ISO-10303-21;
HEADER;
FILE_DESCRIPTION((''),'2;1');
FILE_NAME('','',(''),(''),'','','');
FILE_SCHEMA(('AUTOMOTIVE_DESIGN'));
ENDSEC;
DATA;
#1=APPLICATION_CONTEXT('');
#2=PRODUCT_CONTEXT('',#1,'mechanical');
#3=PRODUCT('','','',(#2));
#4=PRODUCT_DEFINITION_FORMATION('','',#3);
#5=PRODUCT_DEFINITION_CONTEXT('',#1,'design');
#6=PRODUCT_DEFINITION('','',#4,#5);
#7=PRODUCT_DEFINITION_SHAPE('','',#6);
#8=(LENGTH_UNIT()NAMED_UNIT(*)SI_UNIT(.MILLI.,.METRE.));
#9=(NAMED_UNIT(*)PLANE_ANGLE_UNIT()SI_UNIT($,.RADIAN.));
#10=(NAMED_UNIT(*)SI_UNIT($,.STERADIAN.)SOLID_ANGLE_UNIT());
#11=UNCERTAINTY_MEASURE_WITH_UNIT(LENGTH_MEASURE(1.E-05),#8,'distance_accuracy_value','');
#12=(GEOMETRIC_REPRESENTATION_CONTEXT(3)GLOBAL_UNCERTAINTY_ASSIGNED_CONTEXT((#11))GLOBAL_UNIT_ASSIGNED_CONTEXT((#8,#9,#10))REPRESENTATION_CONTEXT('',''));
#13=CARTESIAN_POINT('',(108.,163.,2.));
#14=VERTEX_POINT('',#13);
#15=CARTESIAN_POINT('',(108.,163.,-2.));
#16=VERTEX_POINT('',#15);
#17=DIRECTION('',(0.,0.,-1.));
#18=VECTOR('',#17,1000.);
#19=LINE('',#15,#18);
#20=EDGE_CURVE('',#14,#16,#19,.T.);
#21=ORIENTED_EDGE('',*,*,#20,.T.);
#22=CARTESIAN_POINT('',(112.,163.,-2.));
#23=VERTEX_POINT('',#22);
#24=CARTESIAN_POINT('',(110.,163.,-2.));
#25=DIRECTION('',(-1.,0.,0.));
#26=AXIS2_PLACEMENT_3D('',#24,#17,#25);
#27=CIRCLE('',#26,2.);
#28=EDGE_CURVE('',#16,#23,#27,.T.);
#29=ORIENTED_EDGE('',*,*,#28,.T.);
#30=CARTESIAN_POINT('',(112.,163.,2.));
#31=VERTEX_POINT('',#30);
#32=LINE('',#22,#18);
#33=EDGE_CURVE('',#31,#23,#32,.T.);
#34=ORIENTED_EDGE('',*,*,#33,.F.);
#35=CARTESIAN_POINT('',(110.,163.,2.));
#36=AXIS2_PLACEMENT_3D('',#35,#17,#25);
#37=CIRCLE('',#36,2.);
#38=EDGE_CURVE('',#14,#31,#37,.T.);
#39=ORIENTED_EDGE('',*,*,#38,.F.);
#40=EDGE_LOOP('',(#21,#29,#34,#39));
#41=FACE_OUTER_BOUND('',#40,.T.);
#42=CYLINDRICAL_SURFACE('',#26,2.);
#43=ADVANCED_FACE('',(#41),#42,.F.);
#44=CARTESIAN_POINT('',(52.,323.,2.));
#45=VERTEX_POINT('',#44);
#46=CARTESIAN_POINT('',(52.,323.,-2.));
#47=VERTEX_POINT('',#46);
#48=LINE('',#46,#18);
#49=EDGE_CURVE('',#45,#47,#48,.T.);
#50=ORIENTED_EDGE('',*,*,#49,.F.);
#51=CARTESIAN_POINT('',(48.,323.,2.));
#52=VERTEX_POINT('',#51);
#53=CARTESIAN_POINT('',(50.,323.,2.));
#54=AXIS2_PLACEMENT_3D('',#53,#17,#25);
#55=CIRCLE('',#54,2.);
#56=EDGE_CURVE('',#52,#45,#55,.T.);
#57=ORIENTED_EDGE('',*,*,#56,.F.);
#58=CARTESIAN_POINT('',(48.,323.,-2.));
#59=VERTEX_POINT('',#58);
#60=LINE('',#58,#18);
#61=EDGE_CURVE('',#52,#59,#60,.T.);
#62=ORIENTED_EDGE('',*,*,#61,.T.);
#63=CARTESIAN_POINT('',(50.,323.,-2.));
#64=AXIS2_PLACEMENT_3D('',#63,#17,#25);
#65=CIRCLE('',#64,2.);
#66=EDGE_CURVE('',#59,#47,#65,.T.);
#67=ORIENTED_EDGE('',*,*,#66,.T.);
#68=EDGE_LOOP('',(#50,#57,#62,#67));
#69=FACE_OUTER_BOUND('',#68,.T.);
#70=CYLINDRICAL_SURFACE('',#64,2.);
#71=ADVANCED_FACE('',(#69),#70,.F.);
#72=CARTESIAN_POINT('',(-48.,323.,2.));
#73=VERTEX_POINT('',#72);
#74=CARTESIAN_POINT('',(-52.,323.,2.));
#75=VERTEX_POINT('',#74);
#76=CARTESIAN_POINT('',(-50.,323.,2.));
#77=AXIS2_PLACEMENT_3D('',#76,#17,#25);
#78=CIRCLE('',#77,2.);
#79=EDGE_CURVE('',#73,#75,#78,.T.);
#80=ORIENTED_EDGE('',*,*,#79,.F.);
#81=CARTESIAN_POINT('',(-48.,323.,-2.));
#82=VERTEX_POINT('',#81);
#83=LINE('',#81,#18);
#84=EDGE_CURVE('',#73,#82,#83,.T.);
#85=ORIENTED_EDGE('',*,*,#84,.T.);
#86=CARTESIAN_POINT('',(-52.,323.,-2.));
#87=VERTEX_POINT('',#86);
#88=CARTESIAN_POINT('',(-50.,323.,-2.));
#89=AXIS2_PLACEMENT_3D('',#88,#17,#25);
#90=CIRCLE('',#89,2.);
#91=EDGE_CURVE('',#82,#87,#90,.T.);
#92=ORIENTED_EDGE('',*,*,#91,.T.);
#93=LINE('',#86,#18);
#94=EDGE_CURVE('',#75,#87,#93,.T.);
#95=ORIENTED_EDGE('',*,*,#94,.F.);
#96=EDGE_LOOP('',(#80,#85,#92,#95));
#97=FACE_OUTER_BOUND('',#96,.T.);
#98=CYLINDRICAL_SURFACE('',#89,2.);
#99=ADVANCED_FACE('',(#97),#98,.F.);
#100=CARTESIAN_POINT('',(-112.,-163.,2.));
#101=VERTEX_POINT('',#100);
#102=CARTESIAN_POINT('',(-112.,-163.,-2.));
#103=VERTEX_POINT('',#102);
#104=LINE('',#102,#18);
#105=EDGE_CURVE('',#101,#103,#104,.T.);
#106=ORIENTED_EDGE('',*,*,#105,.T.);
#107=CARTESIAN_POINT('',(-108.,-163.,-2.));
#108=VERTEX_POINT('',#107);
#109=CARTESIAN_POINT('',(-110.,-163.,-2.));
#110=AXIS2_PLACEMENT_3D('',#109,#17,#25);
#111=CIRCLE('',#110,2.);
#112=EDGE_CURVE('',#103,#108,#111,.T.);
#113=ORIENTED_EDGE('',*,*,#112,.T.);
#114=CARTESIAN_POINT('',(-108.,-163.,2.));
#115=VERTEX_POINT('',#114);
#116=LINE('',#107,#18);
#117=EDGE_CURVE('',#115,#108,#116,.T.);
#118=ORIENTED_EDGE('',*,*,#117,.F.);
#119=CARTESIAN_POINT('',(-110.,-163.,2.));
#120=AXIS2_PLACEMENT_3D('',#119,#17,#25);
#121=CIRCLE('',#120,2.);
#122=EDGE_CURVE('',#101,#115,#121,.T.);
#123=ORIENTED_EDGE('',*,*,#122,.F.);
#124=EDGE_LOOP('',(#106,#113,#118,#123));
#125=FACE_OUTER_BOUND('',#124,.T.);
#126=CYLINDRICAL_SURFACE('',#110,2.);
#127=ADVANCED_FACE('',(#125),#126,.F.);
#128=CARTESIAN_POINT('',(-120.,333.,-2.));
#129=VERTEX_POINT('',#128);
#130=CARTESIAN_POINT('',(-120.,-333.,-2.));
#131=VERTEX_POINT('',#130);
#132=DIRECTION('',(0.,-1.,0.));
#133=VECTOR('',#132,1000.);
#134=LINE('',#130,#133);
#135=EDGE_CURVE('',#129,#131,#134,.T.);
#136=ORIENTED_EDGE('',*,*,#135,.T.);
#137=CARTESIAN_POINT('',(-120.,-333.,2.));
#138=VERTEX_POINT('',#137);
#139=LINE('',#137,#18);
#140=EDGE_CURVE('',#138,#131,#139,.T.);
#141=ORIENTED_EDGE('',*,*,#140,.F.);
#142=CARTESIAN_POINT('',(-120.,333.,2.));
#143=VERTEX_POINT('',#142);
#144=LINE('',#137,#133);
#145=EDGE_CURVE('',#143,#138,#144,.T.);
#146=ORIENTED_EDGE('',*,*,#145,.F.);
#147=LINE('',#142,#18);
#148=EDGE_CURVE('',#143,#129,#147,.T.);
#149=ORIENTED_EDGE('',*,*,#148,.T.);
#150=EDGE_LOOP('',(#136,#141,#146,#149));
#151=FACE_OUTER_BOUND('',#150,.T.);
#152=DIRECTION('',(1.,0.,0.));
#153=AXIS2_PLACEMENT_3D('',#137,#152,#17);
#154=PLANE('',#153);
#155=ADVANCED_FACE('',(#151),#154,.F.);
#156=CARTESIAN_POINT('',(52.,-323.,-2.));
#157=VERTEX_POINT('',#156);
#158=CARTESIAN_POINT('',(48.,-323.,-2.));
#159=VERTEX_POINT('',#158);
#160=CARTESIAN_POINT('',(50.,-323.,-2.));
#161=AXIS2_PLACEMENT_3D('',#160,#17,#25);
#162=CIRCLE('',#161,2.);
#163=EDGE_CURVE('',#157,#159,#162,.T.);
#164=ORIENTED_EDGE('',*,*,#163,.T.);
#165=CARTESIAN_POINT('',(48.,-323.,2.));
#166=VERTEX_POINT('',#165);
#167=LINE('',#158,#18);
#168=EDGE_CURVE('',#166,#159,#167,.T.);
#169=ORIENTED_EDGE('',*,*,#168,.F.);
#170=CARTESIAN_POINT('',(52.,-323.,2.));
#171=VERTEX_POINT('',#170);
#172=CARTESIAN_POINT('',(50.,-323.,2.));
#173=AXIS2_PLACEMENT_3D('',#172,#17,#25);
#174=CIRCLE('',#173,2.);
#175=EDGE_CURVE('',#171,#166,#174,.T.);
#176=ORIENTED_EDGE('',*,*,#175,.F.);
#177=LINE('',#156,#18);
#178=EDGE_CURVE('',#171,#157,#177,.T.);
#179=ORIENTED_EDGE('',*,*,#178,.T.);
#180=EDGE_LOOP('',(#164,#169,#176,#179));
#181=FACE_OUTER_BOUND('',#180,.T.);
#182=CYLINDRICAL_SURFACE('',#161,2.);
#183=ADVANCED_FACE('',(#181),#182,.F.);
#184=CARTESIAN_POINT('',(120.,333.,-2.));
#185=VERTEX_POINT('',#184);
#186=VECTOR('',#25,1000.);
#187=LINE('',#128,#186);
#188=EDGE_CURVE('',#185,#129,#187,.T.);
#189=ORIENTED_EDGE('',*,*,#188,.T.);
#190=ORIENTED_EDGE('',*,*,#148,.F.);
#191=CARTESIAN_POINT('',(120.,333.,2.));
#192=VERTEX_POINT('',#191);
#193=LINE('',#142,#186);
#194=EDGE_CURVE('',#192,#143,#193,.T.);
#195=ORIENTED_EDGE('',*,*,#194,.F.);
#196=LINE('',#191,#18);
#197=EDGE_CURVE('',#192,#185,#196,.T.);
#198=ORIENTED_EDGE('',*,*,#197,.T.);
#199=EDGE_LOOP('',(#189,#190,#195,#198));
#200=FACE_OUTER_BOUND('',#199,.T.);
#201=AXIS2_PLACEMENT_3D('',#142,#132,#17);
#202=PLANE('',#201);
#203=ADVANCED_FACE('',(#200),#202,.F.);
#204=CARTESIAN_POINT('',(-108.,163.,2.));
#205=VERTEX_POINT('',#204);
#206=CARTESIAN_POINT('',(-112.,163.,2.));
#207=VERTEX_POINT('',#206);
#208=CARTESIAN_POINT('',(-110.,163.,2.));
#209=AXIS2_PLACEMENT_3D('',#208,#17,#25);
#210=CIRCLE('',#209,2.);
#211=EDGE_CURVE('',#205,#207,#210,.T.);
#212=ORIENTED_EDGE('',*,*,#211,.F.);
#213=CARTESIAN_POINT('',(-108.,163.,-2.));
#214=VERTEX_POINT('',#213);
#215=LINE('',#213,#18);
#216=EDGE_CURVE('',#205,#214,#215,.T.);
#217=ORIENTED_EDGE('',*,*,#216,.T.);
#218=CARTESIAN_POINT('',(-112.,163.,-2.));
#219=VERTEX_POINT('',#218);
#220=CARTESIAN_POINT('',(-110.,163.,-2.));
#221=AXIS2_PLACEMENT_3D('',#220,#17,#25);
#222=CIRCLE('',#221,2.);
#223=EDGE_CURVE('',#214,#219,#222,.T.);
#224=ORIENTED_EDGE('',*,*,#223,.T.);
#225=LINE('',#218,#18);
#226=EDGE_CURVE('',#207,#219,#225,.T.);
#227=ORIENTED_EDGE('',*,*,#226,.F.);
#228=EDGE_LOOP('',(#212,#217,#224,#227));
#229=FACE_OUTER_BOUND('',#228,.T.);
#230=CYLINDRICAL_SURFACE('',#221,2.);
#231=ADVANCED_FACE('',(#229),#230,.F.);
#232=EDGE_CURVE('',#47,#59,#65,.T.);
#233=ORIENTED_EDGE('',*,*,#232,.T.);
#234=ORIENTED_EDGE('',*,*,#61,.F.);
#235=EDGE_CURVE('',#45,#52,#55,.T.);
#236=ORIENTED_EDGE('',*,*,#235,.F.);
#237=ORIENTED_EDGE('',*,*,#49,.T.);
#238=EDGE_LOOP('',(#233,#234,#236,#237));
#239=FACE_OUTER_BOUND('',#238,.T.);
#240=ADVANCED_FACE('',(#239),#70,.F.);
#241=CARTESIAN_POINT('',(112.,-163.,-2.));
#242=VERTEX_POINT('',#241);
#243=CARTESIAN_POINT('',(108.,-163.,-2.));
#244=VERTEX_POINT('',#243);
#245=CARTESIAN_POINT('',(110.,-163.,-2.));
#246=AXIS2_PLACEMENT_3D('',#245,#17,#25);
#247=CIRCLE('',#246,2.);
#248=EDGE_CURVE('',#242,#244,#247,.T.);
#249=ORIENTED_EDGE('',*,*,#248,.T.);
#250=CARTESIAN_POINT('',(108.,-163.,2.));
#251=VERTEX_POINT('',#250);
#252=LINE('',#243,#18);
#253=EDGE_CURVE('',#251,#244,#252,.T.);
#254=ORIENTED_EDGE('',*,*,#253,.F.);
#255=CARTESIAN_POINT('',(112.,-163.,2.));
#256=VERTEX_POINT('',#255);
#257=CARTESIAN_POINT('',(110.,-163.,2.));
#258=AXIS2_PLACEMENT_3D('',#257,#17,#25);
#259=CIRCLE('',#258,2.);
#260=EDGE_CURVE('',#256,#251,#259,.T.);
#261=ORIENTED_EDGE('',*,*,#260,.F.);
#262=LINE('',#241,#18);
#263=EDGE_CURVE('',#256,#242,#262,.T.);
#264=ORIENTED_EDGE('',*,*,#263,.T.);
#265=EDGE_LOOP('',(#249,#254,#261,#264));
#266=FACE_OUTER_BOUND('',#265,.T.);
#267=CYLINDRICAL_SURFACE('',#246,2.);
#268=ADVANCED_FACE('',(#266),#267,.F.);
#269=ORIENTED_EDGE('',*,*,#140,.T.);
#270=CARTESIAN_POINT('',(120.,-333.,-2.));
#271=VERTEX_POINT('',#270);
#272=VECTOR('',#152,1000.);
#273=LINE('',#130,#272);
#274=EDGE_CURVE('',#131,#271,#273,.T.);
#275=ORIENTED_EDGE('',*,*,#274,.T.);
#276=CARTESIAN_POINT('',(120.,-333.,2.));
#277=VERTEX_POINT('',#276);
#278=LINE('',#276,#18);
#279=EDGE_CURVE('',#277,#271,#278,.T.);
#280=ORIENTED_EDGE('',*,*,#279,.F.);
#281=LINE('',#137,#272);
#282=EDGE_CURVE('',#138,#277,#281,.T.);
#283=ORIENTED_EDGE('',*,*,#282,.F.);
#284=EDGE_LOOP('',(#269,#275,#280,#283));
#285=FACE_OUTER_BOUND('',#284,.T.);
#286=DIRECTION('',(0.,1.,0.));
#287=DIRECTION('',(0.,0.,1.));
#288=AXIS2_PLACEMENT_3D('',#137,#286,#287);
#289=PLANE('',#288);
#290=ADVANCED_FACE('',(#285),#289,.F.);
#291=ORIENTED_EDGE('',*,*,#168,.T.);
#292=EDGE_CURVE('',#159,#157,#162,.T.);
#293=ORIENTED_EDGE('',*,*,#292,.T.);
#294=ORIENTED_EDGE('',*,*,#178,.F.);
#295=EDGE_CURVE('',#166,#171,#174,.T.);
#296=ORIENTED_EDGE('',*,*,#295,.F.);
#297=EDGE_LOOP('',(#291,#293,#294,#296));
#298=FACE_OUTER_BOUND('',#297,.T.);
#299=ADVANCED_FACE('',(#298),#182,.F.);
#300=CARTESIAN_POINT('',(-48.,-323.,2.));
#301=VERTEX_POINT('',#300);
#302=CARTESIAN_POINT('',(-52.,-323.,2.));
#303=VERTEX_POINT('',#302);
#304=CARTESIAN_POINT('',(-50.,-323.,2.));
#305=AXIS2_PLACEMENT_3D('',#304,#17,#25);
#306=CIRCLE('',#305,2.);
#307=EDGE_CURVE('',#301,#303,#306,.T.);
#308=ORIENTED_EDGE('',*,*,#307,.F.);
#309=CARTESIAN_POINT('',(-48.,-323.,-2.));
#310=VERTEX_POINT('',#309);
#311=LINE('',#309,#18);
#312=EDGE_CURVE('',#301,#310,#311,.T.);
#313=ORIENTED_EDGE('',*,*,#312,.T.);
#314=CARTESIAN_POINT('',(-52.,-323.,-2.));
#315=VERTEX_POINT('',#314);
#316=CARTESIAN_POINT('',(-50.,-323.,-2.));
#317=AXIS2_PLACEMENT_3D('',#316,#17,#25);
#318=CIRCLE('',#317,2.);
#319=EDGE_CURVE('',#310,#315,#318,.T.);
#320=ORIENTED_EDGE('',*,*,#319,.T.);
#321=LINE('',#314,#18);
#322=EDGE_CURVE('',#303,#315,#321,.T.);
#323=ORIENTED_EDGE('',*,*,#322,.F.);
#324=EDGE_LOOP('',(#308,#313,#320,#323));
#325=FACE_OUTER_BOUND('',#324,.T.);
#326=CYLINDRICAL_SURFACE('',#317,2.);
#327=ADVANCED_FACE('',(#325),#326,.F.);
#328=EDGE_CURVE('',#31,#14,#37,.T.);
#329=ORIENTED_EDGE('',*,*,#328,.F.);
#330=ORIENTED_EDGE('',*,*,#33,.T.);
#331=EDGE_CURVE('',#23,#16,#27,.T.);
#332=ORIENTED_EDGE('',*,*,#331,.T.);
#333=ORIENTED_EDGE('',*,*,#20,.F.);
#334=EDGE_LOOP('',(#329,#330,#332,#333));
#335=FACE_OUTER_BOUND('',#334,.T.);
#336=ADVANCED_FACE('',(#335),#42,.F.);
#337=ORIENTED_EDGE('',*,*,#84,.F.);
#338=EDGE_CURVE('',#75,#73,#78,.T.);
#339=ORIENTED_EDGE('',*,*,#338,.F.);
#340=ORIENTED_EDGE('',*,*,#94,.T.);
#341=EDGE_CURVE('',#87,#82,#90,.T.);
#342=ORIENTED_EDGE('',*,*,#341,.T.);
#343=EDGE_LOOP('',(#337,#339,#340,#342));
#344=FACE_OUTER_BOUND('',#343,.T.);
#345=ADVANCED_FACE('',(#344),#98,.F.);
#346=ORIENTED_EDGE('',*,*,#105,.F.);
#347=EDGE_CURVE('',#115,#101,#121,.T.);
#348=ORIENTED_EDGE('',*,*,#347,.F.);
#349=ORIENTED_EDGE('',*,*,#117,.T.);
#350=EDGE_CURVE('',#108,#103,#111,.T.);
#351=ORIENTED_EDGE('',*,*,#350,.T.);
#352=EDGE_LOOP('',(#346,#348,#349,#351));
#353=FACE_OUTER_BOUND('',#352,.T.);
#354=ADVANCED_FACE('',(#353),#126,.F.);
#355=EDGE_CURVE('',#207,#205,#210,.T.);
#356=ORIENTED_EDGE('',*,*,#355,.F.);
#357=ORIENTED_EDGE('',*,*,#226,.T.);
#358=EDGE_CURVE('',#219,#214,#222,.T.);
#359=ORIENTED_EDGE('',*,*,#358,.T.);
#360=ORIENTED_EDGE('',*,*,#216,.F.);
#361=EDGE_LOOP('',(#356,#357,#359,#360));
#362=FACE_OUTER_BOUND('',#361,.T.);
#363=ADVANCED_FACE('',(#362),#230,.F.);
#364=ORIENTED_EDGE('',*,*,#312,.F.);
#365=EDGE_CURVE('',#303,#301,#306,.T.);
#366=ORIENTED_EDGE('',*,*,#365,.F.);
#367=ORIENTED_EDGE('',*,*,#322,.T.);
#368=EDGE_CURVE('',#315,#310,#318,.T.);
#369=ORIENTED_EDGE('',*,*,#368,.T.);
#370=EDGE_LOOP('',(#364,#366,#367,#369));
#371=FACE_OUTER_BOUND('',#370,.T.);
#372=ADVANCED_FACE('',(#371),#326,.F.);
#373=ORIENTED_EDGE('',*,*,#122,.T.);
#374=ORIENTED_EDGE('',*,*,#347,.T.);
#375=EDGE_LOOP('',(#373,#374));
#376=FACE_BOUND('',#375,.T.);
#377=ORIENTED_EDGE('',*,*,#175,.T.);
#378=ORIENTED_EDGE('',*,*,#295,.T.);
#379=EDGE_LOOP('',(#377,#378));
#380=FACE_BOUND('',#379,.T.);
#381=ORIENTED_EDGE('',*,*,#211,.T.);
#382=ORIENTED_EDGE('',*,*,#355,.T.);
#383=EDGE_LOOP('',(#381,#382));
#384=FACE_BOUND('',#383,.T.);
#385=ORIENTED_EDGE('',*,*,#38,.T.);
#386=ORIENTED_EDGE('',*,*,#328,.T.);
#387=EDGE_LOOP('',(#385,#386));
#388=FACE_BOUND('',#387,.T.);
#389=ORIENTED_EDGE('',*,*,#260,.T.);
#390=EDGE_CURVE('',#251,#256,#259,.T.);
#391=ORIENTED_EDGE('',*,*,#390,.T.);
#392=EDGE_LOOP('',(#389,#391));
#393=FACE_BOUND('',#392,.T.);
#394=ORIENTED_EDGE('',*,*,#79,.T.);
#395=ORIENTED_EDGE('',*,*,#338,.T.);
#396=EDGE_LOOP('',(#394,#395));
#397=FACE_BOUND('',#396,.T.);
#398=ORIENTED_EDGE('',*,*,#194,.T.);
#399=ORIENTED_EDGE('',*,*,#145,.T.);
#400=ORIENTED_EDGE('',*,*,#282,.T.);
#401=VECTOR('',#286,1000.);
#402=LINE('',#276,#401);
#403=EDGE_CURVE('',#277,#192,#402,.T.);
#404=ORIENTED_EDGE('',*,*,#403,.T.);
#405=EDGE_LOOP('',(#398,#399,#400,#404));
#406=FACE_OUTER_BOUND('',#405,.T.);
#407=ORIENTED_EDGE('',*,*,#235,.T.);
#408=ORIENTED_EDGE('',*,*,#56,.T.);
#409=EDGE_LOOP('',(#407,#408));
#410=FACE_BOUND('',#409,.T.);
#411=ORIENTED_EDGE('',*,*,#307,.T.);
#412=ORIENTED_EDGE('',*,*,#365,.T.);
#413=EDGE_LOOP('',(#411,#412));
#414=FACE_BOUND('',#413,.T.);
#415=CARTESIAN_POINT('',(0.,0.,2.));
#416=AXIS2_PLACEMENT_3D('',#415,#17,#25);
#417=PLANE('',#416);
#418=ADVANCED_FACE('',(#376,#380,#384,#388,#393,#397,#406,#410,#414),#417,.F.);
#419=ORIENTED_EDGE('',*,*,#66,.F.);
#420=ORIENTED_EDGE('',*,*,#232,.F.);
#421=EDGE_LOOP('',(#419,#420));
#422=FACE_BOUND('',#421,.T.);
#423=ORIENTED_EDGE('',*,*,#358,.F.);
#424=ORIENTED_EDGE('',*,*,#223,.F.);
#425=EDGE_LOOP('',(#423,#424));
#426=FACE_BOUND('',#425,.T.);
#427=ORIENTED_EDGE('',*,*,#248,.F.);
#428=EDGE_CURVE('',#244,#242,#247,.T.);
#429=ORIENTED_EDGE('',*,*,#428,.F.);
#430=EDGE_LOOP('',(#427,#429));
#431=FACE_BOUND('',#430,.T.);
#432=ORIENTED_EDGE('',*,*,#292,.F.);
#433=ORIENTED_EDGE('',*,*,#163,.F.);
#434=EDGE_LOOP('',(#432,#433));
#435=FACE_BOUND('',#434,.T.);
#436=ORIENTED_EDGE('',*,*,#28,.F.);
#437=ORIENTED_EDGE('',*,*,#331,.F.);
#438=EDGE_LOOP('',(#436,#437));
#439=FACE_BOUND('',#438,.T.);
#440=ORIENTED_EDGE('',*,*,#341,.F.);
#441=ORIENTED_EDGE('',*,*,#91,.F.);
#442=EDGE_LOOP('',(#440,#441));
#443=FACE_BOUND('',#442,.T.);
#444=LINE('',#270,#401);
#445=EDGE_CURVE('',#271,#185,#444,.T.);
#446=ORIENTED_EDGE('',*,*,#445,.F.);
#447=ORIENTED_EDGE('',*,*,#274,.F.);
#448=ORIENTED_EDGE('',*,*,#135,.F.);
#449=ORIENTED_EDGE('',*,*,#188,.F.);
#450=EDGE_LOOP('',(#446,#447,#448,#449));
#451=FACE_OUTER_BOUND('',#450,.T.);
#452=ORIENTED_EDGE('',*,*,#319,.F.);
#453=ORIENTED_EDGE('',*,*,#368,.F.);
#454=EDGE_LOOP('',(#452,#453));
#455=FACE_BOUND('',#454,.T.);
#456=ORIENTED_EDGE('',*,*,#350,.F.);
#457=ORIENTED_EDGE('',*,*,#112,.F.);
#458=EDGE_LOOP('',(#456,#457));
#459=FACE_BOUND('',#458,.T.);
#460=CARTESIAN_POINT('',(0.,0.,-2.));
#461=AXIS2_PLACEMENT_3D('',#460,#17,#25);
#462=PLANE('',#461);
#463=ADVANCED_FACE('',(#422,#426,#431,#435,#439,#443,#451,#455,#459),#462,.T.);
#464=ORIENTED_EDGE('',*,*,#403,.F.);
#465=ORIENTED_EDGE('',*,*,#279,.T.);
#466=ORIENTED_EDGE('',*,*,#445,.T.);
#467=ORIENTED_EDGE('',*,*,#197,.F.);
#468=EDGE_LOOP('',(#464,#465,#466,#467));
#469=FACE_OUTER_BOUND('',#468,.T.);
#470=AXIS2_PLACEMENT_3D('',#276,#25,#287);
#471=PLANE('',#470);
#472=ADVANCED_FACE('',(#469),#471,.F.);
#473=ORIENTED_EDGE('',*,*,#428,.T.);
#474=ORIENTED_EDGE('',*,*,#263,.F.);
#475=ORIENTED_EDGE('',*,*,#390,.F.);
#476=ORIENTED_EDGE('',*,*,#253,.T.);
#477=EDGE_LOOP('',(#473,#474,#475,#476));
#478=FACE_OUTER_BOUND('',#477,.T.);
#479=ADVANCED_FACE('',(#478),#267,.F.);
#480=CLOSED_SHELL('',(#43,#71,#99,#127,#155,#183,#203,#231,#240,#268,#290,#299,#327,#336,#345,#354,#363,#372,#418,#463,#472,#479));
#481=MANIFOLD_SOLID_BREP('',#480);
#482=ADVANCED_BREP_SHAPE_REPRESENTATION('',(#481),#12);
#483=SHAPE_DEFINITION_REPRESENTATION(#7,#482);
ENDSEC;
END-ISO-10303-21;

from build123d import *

# Parameters (mm, degrees)
SKETCH_1_W            = 240
SKETCH_1_H            = 666
EXTRUDE_1_DEPTH       = 2
HOLE_WIZARD_4_0_4_1_D = 4
HOLE_WIZARD_4_0_4_2_D = 4


with BuildPart() as part:
    # 草图1 → 凸台-拉伸1 (new, symmetric)
    with BuildSketch(Plane.XY):
        Rectangle(SKETCH_1_W, SKETCH_1_H)
    extrude(amount=EXTRUDE_1_DEPTH, both=True)

    # Ø4.0 (4) 直径孔1 (through all)
    with Locations(Plane(origin=(0, 0, -2), x_dir=(-1, 0, 0), z_dir=(0, 0, -1))):
        with Locations((-110, 163), (-110, -163)):
            hole_wizard_4_0_4_1 = Hole(HOLE_WIZARD_4_0_4_1_D / 2)

    # Ø4.0 (4) 直径孔2 (through all)
    with Locations(Plane(origin=(0, 0, -2), x_dir=(-1, 0, 0), z_dir=(0, 0, -1))):
        with Locations((-50, 323), (50, 323)):
            hole_wizard_4_0_4_2 = Hole(HOLE_WIZARD_4_0_4_2_D / 2)

    # 镜向1: Ø4.0 (4) 直径孔2 across plane
    add(hole_wizard_4_0_4_2.mirror(Plane.ZX), mode=Mode.SUBTRACT)

    # 镜向2: Ø4.0 (4) 直径孔1 across plane
    add(hole_wizard_4_0_4_1.mirror(Plane(origin=(0, 0, 0), x_dir=(0, 0, 1), z_dir=(1, 0, 0))), mode=Mode.SUBTRACT)


solid = part.part
